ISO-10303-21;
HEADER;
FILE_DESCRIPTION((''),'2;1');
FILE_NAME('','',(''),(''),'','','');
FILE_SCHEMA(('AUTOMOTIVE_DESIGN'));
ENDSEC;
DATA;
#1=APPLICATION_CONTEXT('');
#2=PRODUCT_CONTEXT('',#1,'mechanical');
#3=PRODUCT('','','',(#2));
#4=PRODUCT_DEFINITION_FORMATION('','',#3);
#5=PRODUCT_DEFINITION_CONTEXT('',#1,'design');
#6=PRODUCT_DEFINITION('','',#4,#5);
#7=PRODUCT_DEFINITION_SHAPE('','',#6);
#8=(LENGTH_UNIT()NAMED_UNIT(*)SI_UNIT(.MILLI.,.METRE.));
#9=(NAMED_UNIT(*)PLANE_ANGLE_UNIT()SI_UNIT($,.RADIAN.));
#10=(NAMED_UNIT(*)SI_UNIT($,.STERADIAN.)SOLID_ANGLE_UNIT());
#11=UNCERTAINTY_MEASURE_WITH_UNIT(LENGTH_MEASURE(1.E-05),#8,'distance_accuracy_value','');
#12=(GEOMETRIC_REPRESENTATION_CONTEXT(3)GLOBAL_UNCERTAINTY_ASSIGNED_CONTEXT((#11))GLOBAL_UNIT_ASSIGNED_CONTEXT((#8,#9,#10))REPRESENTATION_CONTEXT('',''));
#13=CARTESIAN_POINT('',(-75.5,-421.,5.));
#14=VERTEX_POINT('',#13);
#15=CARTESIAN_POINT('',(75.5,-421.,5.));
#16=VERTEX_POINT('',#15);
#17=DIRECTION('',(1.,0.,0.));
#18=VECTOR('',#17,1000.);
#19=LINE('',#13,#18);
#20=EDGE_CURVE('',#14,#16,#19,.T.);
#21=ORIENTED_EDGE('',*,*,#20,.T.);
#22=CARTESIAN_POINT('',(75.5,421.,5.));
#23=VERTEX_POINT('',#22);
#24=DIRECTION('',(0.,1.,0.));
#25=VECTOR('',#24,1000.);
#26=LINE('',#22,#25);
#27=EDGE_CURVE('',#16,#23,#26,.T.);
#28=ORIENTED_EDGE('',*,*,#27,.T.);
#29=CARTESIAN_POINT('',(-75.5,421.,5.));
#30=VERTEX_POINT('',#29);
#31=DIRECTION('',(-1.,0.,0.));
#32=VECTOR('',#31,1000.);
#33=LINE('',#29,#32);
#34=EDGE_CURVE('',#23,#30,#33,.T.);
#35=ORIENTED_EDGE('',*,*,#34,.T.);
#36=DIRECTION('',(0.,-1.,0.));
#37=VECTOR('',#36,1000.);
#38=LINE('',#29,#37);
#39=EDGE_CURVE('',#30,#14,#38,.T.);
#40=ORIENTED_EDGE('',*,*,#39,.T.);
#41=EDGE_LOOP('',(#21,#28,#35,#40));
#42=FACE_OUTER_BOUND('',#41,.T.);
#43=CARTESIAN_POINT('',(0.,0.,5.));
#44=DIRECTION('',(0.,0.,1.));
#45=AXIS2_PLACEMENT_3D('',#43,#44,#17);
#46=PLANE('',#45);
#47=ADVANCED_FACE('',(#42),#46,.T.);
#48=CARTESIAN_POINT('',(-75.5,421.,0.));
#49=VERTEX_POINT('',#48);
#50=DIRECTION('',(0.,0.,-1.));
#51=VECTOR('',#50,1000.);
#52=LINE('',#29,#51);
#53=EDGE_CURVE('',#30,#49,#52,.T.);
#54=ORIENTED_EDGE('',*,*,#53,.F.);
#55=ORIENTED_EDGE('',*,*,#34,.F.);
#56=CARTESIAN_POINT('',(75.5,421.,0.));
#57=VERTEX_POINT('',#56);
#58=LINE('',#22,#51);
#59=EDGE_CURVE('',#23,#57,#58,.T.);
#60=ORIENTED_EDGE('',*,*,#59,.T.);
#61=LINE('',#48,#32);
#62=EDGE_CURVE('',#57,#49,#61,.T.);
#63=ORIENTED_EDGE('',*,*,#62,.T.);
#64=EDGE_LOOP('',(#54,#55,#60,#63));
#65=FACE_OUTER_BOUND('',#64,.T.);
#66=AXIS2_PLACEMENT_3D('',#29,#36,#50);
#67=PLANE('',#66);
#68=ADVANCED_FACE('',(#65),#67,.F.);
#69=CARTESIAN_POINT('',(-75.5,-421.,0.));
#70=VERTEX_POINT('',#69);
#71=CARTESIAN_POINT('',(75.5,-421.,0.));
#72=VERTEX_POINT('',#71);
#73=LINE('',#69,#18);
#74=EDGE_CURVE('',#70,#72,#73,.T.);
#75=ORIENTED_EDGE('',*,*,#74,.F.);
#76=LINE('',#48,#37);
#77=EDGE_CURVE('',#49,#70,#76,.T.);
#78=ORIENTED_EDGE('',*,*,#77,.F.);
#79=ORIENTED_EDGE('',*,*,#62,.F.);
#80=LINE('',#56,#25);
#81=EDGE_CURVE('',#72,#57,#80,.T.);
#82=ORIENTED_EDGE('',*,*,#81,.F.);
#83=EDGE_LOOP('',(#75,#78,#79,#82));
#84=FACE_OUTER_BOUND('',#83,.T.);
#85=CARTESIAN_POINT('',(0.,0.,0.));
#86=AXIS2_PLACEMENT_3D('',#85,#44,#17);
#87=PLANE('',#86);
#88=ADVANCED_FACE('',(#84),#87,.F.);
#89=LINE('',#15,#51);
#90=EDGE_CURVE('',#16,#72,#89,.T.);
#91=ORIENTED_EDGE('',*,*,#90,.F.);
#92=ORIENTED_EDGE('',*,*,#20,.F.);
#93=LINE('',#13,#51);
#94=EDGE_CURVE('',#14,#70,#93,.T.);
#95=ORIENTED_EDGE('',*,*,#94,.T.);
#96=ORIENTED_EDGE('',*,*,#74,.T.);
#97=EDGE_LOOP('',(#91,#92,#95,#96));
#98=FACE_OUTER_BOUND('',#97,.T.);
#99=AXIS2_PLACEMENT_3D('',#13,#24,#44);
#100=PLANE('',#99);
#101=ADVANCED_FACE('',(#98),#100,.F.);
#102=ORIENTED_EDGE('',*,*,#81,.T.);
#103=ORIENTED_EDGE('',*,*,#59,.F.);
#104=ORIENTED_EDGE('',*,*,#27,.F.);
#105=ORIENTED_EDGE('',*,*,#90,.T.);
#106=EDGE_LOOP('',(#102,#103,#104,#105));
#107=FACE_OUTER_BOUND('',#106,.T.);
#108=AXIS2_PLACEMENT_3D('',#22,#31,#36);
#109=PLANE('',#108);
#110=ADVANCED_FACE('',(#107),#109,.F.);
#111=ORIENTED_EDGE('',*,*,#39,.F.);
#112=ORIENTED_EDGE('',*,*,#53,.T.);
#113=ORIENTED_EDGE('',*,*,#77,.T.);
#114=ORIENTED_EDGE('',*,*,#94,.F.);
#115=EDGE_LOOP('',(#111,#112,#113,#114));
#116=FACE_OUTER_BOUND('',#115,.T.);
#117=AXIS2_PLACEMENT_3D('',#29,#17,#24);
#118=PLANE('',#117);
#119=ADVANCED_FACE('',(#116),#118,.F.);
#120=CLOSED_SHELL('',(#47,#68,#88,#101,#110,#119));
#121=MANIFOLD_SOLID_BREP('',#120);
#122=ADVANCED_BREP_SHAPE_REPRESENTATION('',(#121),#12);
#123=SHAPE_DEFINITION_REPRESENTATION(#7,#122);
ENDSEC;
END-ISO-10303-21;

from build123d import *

# Parameters (mm, degrees)
SKETCH_1_W      = 151
SKETCH_1_H      = 842
EXTRUDE_1_DEPTH = 5


with BuildPart() as part:
    # 草图1 → 凸台-拉伸1 (new body)
    with BuildSketch(Plane.XY):
        Rectangle(SKETCH_1_W, SKETCH_1_H)
    extrude(amount=EXTRUDE_1_DEPTH)


solid = part.part
